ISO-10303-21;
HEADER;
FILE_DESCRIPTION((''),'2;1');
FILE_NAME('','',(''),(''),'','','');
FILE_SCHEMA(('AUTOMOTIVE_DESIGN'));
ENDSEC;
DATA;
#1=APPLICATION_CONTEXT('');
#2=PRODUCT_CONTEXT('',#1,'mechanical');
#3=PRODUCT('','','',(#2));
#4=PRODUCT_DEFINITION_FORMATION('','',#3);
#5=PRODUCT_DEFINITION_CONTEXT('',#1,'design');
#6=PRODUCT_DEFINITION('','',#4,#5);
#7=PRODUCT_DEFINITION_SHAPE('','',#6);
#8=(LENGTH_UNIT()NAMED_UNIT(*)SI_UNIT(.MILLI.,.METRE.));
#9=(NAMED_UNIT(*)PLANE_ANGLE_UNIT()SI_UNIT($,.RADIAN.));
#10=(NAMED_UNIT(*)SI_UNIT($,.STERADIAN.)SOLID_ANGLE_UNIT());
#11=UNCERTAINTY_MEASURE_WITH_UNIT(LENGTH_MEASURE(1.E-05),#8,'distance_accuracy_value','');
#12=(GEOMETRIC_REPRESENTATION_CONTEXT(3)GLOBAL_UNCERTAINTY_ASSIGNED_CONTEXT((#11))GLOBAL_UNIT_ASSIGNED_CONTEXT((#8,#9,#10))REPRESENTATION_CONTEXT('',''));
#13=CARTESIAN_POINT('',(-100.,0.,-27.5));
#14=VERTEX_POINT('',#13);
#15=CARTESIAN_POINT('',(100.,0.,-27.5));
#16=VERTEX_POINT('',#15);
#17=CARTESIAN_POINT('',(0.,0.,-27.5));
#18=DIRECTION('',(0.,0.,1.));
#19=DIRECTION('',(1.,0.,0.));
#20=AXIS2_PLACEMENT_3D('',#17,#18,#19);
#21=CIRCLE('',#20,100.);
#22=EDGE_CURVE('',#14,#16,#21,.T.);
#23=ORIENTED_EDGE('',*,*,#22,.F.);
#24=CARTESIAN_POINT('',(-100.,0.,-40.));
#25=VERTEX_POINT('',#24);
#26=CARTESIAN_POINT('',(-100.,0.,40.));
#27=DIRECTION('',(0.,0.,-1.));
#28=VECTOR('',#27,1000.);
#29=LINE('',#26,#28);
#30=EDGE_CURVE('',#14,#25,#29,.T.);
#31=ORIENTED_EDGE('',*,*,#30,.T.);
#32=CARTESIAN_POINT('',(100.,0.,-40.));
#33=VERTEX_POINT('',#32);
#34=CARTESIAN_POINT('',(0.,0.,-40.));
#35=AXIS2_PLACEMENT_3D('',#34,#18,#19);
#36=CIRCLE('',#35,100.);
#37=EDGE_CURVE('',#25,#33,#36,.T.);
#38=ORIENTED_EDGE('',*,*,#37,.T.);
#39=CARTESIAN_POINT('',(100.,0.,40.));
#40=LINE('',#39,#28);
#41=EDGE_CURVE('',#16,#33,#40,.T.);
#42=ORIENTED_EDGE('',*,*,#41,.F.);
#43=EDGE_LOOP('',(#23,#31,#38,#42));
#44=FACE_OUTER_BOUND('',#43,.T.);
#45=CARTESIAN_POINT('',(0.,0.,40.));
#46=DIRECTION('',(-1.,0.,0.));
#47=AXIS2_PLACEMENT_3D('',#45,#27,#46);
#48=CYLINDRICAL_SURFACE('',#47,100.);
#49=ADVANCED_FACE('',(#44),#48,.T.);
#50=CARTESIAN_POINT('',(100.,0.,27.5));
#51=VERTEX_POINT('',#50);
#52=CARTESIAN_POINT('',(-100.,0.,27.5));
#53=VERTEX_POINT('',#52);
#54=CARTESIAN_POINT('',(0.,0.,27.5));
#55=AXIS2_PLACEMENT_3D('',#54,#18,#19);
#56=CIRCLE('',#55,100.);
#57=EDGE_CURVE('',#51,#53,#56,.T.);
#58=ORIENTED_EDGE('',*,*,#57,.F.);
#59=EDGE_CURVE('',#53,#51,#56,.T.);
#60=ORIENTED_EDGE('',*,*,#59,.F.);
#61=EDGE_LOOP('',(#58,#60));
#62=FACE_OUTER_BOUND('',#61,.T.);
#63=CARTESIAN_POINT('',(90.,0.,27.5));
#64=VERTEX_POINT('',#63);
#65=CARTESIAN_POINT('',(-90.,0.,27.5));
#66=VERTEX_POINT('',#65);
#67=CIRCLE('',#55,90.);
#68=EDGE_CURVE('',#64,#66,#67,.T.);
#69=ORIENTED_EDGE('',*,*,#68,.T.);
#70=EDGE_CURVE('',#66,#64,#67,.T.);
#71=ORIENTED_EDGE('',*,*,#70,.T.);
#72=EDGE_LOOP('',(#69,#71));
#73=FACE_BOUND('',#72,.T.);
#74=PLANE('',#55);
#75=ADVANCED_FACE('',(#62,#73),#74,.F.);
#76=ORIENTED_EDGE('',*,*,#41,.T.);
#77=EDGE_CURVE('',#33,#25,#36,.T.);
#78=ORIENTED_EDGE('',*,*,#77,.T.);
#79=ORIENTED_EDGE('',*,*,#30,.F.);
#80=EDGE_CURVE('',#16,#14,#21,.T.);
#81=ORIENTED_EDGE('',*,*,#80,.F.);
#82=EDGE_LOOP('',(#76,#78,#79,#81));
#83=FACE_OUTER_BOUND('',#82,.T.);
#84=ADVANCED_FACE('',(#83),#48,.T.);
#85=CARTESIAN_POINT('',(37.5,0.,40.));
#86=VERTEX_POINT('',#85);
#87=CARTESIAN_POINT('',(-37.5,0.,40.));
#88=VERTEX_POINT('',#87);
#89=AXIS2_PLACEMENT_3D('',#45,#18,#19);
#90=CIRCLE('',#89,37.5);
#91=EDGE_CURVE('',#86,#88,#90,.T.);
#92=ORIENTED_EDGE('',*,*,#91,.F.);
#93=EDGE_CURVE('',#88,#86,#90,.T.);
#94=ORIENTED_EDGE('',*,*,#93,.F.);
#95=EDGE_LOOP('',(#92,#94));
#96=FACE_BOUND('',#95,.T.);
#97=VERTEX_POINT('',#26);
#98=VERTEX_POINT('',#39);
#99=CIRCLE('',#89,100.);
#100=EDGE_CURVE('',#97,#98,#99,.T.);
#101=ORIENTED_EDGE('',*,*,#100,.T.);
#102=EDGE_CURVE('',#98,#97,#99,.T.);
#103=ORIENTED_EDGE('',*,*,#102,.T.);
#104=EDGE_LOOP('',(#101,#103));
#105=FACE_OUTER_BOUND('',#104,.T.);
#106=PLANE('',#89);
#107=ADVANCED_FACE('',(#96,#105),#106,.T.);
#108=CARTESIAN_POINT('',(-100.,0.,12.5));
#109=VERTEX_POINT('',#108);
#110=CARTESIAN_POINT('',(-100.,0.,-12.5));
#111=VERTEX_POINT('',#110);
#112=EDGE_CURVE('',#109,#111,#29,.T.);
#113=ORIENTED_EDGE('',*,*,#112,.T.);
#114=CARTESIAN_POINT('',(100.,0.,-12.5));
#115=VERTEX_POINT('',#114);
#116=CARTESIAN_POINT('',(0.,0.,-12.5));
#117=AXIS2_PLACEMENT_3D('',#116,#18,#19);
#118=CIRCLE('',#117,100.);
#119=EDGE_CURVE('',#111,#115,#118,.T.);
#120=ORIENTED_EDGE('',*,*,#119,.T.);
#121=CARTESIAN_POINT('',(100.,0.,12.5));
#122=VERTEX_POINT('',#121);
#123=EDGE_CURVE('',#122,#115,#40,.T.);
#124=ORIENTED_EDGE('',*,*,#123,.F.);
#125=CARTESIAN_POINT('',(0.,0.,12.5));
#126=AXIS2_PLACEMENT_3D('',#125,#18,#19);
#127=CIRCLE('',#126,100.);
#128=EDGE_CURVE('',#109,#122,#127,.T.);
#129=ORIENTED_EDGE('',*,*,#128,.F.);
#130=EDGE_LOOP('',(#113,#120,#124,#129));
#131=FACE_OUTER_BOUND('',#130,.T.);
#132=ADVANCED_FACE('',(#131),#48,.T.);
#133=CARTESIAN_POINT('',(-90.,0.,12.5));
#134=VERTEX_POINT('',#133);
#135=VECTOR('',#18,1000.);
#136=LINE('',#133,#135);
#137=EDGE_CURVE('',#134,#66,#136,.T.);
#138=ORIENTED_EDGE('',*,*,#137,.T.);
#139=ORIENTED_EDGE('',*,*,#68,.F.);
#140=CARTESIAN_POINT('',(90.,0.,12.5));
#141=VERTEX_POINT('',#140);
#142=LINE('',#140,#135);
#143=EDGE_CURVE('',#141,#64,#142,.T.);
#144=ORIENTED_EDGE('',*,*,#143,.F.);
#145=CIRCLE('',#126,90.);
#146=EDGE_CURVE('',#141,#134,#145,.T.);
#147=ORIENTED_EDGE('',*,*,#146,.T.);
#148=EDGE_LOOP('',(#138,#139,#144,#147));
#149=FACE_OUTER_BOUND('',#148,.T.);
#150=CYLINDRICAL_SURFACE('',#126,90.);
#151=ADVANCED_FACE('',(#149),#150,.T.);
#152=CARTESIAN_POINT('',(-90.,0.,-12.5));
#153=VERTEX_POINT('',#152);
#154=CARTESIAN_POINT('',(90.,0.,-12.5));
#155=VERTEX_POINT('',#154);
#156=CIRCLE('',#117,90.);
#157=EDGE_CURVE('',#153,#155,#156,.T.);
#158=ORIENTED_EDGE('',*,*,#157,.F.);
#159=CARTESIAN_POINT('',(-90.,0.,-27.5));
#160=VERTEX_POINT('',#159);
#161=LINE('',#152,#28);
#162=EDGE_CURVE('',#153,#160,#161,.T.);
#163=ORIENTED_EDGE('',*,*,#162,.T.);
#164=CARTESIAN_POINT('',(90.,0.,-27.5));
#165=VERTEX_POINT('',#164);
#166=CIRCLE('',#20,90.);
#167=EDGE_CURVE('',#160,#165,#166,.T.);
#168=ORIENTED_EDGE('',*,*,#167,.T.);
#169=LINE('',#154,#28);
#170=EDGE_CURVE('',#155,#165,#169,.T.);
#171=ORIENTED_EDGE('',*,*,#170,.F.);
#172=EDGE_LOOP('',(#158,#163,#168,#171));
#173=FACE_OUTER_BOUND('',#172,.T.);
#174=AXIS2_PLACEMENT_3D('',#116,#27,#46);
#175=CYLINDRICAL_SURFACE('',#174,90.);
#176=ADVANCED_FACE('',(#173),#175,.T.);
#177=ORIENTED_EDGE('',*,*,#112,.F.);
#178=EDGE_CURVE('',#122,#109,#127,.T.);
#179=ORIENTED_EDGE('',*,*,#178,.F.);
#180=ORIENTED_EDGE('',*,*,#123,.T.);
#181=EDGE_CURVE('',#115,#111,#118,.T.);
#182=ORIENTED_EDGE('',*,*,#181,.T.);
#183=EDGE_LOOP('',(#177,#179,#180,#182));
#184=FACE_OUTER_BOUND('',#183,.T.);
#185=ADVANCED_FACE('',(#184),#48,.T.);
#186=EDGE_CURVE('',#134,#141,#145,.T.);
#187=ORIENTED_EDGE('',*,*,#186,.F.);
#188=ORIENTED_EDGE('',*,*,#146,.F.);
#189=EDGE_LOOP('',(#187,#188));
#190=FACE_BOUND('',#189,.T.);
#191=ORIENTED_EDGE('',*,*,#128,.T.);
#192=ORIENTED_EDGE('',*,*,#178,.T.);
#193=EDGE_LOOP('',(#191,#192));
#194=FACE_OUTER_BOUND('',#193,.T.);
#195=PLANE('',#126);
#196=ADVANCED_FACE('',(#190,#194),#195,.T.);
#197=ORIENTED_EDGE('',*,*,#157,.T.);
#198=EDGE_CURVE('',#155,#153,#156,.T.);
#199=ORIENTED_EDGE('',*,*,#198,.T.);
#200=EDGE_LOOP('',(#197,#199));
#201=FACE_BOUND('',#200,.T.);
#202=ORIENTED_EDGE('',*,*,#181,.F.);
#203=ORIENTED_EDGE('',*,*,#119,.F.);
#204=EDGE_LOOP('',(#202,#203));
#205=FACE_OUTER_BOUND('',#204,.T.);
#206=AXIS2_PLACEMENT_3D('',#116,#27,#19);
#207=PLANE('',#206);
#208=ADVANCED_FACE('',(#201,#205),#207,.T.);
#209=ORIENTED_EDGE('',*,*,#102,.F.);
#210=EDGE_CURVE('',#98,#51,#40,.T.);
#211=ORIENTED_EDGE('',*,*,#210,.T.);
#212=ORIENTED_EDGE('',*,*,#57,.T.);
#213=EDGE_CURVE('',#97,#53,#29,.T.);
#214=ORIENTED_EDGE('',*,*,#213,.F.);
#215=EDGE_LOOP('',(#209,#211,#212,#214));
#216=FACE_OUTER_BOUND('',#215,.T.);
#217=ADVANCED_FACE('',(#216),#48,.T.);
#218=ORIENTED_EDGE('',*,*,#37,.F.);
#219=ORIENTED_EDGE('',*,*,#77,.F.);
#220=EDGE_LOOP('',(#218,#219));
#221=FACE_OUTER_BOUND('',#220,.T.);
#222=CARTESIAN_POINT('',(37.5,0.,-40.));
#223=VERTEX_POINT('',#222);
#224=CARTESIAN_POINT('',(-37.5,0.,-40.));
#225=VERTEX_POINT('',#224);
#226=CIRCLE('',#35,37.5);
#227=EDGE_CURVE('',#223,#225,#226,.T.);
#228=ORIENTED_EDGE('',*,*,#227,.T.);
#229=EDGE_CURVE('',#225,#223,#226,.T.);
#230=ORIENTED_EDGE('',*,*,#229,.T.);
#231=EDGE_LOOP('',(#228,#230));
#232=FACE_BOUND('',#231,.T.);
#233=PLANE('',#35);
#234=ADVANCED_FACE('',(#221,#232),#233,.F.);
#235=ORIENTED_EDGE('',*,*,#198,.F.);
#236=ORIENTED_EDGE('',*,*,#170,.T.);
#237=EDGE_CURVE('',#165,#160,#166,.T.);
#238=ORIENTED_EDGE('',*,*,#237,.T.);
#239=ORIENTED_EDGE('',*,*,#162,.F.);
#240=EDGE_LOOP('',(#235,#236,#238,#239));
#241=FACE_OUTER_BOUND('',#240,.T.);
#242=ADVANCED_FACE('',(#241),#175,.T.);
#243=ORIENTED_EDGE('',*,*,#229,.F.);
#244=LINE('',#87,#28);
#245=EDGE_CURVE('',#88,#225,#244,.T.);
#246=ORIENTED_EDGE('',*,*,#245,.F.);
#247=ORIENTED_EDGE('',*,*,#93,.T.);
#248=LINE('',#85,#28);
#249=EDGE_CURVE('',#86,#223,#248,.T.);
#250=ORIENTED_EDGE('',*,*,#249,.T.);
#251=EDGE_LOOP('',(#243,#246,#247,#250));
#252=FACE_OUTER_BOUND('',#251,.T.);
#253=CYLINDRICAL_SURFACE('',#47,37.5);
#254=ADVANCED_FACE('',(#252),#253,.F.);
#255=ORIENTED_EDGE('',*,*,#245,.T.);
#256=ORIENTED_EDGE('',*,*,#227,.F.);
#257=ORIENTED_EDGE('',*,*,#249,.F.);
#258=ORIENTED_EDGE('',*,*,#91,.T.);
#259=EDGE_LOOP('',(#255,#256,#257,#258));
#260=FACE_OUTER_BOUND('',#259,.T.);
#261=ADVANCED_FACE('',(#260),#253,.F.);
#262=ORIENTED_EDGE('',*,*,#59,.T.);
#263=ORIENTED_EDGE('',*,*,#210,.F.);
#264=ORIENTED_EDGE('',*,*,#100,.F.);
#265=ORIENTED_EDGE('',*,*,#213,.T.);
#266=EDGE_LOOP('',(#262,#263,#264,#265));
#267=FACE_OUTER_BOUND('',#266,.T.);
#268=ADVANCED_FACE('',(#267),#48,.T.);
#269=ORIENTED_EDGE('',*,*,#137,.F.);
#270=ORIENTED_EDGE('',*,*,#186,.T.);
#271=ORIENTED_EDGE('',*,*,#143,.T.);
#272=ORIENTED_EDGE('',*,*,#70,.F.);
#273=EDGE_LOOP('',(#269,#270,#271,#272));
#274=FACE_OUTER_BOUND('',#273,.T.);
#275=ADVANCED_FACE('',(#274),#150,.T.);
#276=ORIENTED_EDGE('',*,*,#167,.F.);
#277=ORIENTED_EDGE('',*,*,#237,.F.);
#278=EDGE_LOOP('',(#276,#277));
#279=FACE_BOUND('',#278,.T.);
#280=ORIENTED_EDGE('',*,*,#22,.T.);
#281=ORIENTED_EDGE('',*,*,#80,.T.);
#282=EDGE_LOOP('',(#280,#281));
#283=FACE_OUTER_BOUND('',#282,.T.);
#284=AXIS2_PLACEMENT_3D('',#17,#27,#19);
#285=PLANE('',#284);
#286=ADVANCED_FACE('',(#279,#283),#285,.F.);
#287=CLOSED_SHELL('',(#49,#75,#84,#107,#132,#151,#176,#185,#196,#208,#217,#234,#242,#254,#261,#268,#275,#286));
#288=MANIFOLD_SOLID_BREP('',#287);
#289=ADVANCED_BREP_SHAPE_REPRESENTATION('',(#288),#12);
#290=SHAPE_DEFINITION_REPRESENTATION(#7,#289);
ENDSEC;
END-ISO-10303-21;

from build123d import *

# Parameters (mm, degrees)
SKETCH_1_R          = 100
SKETCH_1_R_2        = 37.5
EXTRUDE_1_DEPTH     = 40
SKETCH_2_R          = 100
SKETCH_2_R_2        = 90
CUT_EXTRUDE_1_DEPTH = 7.5


with BuildPart() as part:
    # 草图1 → 凸台-拉伸1 (new, symmetric)
    with BuildSketch(Plane.XY):
        Circle(SKETCH_1_R)
        Circle(SKETCH_1_R_2, mode=Mode.SUBTRACT)
    extrude(amount=EXTRUDE_1_DEPTH, both=True)

    # 草图2 → 切除-拉伸1 (cut, symmetric)
    with BuildSketch(Plane.XY.offset(20)):
        Circle(SKETCH_2_R)
        Circle(SKETCH_2_R_2, mode=Mode.SUBTRACT)
    cut_extrude_1 = extrude(amount=CUT_EXTRUDE_1_DEPTH, both=True, mode=Mode.SUBTRACT)

    # 镜向1: 切除-拉伸1 across plane
    add(cut_extrude_1.mirror(Plane.XY), mode=Mode.SUBTRACT)


solid = part.part
